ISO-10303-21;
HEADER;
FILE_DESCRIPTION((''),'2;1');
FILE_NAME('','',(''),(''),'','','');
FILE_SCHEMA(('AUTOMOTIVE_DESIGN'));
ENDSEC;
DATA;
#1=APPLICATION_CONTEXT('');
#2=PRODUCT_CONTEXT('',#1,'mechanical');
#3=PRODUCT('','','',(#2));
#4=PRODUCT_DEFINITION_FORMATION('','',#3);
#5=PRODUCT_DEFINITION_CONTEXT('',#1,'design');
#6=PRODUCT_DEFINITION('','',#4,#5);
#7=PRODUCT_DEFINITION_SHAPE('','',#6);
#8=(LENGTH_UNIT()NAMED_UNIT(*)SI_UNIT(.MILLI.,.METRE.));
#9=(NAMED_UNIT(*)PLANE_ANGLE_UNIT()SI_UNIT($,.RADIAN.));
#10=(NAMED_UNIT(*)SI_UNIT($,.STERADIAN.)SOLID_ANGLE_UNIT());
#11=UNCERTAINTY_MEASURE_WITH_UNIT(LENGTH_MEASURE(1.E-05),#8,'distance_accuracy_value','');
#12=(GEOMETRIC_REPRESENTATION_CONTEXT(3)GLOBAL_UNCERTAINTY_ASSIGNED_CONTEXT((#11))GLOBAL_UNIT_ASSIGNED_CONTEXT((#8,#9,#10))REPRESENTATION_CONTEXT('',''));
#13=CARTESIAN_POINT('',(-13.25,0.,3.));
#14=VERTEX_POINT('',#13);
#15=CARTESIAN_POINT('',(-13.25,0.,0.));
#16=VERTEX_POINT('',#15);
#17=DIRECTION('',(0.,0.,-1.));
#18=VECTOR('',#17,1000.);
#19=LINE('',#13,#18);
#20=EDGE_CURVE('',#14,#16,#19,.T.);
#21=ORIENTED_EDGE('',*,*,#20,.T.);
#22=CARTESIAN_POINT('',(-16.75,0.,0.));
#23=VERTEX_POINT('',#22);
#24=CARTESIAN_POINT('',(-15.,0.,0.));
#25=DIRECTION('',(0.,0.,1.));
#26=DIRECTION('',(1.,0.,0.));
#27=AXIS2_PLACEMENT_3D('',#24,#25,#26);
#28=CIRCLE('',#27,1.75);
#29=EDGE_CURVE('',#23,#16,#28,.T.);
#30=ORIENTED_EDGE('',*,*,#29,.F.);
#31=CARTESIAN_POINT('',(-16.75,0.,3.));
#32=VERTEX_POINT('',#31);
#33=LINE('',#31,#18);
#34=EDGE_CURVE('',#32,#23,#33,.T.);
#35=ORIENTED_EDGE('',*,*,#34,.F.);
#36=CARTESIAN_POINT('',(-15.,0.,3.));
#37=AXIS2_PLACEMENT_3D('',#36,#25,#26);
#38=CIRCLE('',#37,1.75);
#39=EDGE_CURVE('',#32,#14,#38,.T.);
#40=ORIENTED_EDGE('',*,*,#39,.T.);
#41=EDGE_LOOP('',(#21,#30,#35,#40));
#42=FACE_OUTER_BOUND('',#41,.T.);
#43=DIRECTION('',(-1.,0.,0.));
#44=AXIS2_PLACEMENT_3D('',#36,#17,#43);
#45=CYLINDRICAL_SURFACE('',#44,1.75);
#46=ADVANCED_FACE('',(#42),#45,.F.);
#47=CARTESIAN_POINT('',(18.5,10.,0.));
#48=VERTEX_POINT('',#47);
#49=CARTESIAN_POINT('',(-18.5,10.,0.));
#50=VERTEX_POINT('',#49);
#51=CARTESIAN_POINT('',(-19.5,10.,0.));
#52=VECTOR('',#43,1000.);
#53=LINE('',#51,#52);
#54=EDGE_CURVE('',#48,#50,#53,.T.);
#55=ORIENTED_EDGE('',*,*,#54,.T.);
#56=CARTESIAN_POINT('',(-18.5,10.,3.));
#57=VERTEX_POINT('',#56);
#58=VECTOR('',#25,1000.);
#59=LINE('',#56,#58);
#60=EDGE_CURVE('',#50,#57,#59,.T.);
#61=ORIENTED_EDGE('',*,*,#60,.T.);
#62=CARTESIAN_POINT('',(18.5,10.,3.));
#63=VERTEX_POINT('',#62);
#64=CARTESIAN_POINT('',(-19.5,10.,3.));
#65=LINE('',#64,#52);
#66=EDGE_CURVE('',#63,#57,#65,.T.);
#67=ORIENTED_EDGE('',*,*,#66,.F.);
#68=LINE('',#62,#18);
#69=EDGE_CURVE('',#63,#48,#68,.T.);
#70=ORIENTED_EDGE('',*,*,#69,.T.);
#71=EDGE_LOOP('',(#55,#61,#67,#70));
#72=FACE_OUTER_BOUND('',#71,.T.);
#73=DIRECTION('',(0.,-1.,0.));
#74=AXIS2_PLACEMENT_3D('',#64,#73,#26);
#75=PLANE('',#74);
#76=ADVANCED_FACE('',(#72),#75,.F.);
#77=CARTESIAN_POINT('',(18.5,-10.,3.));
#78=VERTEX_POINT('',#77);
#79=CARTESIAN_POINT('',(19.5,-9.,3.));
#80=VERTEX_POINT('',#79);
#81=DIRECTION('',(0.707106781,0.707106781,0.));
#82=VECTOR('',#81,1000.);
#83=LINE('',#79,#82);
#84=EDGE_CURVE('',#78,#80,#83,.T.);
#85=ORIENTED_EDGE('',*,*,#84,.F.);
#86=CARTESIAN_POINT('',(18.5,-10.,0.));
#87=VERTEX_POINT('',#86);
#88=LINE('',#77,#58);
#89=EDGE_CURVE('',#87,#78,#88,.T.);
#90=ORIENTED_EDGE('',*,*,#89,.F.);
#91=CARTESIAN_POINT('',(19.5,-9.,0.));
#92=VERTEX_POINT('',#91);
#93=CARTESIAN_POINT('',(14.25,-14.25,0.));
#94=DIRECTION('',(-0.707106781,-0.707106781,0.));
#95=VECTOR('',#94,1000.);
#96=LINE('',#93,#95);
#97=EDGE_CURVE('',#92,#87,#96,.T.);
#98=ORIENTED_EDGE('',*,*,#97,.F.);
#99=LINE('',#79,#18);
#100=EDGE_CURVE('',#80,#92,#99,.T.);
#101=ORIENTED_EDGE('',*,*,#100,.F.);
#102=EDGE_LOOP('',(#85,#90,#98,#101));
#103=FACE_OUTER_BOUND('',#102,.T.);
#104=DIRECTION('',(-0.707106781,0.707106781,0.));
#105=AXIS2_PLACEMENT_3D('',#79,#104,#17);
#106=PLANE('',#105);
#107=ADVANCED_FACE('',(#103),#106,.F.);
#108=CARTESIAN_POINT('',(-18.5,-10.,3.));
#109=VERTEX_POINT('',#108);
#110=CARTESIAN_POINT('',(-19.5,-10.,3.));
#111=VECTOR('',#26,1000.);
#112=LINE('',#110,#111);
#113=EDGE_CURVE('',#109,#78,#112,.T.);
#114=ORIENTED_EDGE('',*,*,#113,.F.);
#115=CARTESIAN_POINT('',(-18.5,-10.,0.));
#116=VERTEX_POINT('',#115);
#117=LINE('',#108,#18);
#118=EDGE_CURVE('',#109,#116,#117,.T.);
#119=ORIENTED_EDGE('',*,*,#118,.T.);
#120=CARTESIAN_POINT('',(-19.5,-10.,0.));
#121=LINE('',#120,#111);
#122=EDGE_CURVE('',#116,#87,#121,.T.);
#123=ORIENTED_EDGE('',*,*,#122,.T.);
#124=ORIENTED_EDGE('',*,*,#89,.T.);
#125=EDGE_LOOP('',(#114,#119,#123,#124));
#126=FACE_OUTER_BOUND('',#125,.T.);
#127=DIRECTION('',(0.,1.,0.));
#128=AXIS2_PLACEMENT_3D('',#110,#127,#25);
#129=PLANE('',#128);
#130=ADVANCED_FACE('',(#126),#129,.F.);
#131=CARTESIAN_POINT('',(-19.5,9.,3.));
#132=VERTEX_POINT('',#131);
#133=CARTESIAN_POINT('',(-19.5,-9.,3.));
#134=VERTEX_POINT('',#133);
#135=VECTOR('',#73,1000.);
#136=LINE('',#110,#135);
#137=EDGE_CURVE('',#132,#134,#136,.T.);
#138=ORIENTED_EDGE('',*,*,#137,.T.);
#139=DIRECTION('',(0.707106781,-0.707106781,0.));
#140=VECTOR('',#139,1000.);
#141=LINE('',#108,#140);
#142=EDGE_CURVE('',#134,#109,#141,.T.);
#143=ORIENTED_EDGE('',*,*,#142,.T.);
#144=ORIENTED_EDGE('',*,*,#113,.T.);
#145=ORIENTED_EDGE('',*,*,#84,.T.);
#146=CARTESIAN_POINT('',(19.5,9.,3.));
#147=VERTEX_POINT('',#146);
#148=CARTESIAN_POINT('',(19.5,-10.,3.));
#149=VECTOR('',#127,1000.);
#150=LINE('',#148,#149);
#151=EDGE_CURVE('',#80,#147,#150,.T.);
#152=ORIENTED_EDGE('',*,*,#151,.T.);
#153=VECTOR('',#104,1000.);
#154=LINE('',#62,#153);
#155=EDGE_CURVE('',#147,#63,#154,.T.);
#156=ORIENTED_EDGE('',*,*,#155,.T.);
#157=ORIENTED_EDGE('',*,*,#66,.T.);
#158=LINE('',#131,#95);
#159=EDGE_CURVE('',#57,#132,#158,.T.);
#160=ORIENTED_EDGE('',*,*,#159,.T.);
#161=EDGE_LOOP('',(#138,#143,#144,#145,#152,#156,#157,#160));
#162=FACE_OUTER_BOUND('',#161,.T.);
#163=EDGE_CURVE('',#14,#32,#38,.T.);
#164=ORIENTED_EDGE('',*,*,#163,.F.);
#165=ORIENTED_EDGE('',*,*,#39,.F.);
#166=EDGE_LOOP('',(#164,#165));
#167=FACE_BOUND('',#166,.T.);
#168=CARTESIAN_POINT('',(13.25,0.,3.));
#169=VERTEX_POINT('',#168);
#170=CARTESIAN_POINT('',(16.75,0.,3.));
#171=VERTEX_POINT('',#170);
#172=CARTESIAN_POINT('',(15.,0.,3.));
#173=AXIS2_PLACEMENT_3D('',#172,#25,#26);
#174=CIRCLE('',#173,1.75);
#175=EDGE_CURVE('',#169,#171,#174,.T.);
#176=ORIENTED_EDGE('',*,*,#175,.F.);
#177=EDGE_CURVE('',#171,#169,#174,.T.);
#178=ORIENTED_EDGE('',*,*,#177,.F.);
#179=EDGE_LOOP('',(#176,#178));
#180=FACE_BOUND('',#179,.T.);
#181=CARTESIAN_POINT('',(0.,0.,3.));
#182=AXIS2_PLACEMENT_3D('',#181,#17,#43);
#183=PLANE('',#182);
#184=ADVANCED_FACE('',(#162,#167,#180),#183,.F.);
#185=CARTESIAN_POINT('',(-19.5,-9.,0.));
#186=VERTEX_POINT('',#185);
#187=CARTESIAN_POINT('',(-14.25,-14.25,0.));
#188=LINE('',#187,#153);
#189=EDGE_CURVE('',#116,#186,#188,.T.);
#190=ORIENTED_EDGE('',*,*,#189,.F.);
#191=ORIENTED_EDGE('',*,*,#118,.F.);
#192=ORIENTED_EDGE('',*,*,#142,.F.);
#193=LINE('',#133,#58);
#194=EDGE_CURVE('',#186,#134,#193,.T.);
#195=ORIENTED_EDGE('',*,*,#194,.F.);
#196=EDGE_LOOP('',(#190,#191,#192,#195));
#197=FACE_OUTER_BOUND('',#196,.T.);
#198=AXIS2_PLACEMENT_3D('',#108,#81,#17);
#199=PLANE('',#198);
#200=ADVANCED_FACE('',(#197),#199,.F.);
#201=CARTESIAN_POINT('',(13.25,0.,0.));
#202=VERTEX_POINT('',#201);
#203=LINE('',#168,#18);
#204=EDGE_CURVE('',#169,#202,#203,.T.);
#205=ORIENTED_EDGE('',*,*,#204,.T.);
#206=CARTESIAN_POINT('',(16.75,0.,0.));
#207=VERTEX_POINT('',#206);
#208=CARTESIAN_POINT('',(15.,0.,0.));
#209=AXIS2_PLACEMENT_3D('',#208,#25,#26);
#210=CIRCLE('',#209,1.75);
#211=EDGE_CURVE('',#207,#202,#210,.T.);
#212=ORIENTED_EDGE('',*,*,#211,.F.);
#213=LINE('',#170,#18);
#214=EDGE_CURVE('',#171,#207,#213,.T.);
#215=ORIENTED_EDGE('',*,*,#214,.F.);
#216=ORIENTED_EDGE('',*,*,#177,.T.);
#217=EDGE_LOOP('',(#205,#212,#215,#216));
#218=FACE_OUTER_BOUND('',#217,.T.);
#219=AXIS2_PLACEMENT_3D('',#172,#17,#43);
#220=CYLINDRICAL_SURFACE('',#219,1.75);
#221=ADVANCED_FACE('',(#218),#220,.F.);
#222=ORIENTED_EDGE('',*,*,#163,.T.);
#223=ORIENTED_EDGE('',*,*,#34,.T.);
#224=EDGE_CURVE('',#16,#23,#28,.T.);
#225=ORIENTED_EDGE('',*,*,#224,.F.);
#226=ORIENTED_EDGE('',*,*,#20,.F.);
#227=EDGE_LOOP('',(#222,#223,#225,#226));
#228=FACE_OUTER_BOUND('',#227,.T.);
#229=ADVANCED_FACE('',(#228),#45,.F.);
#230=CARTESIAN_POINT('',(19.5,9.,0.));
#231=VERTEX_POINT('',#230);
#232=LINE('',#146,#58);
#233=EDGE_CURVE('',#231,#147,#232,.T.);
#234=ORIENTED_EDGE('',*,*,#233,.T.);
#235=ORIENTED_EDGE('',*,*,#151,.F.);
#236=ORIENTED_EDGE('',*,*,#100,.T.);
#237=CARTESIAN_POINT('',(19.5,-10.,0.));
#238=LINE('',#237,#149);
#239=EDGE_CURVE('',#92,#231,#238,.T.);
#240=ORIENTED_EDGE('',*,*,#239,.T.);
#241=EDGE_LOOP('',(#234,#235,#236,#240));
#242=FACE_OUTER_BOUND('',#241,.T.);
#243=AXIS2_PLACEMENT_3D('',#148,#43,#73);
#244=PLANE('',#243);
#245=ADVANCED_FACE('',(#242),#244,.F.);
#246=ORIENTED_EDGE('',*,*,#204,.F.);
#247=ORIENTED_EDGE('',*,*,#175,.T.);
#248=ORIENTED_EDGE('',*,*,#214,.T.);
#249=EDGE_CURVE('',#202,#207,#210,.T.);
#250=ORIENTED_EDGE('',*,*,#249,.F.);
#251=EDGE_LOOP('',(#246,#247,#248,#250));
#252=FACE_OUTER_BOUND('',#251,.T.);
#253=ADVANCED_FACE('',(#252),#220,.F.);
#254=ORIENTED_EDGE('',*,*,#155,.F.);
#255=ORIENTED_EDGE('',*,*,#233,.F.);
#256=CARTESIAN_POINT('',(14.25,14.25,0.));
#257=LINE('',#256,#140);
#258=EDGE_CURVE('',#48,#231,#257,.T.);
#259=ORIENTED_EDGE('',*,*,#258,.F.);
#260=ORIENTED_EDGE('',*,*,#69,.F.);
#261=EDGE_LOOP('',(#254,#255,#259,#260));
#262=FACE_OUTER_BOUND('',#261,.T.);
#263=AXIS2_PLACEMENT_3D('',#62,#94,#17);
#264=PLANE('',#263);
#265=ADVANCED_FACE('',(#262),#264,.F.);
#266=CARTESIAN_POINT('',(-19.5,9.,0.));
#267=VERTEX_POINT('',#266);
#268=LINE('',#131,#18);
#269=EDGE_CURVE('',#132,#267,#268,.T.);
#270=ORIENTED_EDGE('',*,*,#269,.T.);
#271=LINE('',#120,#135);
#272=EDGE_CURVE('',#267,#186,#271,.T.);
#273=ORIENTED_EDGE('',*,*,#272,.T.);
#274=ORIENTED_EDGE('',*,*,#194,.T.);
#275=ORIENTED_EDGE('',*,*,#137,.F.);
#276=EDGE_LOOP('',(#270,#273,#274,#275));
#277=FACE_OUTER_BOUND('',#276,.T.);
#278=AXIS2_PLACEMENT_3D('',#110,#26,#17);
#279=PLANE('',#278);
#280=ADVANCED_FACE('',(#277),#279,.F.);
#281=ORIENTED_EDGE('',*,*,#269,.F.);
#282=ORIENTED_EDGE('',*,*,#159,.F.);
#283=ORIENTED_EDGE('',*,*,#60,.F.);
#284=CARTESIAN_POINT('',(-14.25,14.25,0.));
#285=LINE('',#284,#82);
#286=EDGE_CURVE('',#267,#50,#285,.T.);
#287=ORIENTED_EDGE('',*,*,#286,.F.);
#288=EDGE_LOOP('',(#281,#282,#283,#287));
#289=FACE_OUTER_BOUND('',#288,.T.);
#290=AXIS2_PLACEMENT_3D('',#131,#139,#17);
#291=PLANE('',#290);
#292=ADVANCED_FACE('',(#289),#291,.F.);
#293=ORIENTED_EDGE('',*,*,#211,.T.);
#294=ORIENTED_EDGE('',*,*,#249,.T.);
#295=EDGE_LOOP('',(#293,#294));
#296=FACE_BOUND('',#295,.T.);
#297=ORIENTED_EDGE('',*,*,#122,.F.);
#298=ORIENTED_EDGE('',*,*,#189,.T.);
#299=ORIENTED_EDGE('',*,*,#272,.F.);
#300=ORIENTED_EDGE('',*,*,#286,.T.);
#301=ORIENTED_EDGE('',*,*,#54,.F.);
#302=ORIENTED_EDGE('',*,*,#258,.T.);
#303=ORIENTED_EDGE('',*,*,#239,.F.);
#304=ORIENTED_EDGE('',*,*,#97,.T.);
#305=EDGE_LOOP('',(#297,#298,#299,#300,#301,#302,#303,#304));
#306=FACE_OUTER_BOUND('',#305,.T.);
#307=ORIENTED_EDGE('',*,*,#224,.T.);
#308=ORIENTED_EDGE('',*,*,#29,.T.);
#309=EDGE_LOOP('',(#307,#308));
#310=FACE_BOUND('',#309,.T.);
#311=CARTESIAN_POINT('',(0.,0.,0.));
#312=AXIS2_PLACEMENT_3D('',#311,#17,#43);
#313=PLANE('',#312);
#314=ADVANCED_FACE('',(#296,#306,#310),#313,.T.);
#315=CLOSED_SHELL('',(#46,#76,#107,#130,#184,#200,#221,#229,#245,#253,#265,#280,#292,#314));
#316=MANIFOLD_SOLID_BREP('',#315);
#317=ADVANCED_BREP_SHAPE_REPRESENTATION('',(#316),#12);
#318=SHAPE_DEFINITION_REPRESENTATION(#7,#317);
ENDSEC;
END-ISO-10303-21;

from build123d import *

# Parameters (mm, degrees)
SKETCH1_W           = 39
SKETCH1_H           = 20
SKETCH1_R           = 1.75
BOSS_EXTRUDE1_DEPTH = 3
CHAMFER1_SIZE       = 1


with BuildPart() as part:
    # Sketch1 → Boss-Extrude1 (new body)
    with BuildSketch(Plane.XY):
        Rectangle(SKETCH1_W, SKETCH1_H)
        with Locations((-15, 0)):
            Circle(SKETCH1_R, mode=Mode.SUBTRACT)
        with Locations((15, 0)):
            Circle(SKETCH1_R, mode=Mode.SUBTRACT)
    extrude(amount=BOSS_EXTRUDE1_DEPTH)

    # Chamfer1
    chamfer1_edges = [part.edges().sort_by_distance(p)[0] for p in [
        (19.5, -10, 1.5),
        (-19.5, -10, 1.5),
        (-19.5, 10, 1.5),
        (19.5, 10, 1.5),
    ]]
    chamfer(chamfer1_edges, length=CHAMFER1_SIZE)


solid = part.part
